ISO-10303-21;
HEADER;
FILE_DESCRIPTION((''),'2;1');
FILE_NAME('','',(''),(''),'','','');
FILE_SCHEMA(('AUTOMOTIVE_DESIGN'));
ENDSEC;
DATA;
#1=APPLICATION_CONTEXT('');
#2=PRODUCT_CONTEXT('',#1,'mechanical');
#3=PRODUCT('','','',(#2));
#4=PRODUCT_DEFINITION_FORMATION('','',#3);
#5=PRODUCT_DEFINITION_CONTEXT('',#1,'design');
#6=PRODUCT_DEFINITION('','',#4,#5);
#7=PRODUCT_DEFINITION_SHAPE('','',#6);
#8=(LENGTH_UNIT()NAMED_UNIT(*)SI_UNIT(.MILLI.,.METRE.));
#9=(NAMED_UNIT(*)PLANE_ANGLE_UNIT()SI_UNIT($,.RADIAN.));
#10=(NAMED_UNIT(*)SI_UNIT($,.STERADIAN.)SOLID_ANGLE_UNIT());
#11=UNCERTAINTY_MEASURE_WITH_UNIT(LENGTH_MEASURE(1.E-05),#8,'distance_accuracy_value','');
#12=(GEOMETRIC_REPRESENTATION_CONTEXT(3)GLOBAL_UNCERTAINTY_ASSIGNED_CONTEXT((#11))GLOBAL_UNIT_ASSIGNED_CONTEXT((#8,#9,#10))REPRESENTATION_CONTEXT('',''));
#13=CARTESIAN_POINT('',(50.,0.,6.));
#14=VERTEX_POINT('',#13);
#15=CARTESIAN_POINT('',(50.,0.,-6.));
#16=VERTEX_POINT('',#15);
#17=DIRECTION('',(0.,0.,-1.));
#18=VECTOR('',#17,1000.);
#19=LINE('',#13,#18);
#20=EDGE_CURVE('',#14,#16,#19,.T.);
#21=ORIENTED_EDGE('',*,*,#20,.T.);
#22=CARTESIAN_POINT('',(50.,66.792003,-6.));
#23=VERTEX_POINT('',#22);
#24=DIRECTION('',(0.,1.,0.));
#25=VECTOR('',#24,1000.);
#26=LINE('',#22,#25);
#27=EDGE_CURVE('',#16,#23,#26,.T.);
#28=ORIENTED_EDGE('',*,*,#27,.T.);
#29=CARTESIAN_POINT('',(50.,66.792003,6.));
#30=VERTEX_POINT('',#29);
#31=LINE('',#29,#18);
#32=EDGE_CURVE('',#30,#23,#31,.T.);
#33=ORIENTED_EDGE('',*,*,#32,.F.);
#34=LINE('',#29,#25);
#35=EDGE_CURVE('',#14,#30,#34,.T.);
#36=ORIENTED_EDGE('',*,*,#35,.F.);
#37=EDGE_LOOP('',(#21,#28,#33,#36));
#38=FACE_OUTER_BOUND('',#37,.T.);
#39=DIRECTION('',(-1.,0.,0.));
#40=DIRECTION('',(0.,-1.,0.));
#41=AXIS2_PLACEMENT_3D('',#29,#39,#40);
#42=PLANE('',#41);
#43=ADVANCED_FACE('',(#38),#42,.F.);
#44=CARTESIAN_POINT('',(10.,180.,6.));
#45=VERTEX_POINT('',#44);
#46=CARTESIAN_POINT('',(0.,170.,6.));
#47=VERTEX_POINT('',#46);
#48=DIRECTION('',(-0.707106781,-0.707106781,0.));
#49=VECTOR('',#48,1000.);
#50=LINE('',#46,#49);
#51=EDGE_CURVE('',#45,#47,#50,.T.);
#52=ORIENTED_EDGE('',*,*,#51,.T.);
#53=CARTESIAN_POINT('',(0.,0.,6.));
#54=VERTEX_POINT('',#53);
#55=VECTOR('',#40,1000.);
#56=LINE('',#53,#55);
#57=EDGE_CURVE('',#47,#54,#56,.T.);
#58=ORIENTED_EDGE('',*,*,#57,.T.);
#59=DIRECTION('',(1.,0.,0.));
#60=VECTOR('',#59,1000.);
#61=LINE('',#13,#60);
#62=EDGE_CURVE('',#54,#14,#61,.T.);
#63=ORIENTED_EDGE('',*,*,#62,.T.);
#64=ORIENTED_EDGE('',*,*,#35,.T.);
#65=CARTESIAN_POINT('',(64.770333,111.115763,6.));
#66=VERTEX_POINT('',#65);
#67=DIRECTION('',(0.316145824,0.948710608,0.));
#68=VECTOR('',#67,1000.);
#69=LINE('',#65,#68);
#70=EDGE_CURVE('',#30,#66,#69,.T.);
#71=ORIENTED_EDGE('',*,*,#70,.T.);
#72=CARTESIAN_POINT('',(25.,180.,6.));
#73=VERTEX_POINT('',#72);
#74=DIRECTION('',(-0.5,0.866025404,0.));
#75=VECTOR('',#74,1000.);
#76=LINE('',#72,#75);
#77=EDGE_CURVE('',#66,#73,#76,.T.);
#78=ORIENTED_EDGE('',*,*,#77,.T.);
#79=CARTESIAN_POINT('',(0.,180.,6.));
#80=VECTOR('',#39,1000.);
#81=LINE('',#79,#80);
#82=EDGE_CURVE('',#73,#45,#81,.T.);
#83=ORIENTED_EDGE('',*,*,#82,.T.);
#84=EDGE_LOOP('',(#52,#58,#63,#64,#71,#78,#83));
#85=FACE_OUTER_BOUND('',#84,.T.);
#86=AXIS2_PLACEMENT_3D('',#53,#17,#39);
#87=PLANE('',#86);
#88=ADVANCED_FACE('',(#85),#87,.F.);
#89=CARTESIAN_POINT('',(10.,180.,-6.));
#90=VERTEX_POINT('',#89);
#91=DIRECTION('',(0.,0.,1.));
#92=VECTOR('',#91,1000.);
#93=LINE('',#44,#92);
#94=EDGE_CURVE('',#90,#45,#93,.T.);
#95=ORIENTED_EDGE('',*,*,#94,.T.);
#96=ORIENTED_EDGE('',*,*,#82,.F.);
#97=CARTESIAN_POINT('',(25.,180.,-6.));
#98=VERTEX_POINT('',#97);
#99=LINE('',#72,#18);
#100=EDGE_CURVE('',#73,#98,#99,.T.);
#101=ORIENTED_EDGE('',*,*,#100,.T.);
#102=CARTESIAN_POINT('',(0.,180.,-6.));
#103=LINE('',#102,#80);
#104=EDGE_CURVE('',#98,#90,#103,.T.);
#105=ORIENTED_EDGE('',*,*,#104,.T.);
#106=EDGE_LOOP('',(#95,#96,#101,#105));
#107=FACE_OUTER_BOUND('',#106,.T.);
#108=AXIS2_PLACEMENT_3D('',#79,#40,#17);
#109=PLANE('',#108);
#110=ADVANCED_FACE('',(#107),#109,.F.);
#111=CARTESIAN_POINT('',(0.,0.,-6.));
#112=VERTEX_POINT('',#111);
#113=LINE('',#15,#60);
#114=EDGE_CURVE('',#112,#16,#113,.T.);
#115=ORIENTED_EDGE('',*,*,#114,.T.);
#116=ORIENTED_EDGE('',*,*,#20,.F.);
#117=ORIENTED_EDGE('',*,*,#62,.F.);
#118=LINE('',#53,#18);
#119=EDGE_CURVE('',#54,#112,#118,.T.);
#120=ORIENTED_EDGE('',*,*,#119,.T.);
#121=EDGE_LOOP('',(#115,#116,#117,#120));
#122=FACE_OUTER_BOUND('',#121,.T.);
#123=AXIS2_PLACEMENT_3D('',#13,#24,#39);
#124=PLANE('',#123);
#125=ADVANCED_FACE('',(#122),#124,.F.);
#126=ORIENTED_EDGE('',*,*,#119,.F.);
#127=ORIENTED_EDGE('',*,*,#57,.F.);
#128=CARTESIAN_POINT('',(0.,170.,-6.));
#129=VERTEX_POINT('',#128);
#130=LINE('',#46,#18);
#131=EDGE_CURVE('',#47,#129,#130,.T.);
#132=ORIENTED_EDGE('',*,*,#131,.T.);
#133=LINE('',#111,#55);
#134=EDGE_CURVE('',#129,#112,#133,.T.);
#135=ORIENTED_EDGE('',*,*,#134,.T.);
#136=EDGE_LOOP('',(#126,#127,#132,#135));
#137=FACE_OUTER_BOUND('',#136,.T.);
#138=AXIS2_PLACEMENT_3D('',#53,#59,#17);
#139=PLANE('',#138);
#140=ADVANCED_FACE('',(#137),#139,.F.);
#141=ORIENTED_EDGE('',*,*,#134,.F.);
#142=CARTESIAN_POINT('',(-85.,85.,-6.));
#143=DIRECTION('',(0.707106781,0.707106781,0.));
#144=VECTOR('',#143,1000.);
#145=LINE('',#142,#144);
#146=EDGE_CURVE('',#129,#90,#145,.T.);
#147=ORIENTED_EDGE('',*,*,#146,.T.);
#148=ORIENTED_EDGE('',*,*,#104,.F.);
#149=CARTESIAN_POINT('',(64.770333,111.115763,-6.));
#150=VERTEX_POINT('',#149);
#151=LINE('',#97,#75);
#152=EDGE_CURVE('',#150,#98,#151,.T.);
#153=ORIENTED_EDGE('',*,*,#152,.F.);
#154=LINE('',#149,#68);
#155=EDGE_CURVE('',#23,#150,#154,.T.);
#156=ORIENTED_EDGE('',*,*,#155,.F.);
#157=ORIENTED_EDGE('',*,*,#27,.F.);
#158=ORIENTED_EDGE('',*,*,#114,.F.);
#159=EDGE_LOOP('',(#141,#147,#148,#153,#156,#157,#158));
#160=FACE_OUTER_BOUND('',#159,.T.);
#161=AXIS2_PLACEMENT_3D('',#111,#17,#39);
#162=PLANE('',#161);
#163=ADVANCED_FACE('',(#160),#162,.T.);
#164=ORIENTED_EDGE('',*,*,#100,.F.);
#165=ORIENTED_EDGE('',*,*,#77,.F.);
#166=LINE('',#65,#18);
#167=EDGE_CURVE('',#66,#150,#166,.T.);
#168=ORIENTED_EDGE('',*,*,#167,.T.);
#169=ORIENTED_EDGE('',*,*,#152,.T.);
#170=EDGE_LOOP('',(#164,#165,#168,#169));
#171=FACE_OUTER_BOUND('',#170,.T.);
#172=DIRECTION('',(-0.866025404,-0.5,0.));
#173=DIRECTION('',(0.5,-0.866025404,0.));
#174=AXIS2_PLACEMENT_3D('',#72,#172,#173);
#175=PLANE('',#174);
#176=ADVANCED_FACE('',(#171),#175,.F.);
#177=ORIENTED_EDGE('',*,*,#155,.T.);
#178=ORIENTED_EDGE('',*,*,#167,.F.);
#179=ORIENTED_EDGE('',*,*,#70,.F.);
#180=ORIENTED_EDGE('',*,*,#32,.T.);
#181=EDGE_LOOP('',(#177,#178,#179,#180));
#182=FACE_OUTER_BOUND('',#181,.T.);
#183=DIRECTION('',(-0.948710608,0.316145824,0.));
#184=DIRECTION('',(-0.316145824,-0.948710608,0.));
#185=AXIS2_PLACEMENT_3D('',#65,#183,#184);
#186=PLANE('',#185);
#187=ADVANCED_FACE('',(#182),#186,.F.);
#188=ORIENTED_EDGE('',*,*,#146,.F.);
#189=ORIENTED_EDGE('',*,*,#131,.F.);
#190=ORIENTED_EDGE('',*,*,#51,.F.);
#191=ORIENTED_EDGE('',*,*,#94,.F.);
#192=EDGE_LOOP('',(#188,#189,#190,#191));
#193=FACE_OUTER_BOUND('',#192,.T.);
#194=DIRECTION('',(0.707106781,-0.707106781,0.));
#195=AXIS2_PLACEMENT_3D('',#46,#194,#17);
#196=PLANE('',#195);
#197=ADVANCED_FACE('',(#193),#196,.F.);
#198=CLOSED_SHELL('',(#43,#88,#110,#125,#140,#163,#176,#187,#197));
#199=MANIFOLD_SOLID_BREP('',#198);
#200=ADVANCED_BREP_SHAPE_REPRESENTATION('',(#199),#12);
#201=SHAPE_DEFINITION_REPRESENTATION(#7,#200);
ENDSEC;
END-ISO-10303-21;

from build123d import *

# Parameters (mm, degrees)
BOSS_EXTRUDE1_DEPTH = 6
CHAMFER1_SIZE       = 10


with BuildPart() as part:
    # Sketch1 → Boss-Extrude1 (new, symmetric)
    with BuildSketch(Plane.XY):
        Polygon((0, 0), (0, 180), (25, 180), (64.770332896, 111.11576279), (50, 66.792003178), (50, 0), align=None)
    extrude(amount=BOSS_EXTRUDE1_DEPTH, both=True)

    # Chamfer1
    chamfer1_edges = [part.edges().sort_by_distance(p)[0] for p in [
        (0, 180, 0),
    ]]
    chamfer(chamfer1_edges, length=CHAMFER1_SIZE)


solid = part.part
